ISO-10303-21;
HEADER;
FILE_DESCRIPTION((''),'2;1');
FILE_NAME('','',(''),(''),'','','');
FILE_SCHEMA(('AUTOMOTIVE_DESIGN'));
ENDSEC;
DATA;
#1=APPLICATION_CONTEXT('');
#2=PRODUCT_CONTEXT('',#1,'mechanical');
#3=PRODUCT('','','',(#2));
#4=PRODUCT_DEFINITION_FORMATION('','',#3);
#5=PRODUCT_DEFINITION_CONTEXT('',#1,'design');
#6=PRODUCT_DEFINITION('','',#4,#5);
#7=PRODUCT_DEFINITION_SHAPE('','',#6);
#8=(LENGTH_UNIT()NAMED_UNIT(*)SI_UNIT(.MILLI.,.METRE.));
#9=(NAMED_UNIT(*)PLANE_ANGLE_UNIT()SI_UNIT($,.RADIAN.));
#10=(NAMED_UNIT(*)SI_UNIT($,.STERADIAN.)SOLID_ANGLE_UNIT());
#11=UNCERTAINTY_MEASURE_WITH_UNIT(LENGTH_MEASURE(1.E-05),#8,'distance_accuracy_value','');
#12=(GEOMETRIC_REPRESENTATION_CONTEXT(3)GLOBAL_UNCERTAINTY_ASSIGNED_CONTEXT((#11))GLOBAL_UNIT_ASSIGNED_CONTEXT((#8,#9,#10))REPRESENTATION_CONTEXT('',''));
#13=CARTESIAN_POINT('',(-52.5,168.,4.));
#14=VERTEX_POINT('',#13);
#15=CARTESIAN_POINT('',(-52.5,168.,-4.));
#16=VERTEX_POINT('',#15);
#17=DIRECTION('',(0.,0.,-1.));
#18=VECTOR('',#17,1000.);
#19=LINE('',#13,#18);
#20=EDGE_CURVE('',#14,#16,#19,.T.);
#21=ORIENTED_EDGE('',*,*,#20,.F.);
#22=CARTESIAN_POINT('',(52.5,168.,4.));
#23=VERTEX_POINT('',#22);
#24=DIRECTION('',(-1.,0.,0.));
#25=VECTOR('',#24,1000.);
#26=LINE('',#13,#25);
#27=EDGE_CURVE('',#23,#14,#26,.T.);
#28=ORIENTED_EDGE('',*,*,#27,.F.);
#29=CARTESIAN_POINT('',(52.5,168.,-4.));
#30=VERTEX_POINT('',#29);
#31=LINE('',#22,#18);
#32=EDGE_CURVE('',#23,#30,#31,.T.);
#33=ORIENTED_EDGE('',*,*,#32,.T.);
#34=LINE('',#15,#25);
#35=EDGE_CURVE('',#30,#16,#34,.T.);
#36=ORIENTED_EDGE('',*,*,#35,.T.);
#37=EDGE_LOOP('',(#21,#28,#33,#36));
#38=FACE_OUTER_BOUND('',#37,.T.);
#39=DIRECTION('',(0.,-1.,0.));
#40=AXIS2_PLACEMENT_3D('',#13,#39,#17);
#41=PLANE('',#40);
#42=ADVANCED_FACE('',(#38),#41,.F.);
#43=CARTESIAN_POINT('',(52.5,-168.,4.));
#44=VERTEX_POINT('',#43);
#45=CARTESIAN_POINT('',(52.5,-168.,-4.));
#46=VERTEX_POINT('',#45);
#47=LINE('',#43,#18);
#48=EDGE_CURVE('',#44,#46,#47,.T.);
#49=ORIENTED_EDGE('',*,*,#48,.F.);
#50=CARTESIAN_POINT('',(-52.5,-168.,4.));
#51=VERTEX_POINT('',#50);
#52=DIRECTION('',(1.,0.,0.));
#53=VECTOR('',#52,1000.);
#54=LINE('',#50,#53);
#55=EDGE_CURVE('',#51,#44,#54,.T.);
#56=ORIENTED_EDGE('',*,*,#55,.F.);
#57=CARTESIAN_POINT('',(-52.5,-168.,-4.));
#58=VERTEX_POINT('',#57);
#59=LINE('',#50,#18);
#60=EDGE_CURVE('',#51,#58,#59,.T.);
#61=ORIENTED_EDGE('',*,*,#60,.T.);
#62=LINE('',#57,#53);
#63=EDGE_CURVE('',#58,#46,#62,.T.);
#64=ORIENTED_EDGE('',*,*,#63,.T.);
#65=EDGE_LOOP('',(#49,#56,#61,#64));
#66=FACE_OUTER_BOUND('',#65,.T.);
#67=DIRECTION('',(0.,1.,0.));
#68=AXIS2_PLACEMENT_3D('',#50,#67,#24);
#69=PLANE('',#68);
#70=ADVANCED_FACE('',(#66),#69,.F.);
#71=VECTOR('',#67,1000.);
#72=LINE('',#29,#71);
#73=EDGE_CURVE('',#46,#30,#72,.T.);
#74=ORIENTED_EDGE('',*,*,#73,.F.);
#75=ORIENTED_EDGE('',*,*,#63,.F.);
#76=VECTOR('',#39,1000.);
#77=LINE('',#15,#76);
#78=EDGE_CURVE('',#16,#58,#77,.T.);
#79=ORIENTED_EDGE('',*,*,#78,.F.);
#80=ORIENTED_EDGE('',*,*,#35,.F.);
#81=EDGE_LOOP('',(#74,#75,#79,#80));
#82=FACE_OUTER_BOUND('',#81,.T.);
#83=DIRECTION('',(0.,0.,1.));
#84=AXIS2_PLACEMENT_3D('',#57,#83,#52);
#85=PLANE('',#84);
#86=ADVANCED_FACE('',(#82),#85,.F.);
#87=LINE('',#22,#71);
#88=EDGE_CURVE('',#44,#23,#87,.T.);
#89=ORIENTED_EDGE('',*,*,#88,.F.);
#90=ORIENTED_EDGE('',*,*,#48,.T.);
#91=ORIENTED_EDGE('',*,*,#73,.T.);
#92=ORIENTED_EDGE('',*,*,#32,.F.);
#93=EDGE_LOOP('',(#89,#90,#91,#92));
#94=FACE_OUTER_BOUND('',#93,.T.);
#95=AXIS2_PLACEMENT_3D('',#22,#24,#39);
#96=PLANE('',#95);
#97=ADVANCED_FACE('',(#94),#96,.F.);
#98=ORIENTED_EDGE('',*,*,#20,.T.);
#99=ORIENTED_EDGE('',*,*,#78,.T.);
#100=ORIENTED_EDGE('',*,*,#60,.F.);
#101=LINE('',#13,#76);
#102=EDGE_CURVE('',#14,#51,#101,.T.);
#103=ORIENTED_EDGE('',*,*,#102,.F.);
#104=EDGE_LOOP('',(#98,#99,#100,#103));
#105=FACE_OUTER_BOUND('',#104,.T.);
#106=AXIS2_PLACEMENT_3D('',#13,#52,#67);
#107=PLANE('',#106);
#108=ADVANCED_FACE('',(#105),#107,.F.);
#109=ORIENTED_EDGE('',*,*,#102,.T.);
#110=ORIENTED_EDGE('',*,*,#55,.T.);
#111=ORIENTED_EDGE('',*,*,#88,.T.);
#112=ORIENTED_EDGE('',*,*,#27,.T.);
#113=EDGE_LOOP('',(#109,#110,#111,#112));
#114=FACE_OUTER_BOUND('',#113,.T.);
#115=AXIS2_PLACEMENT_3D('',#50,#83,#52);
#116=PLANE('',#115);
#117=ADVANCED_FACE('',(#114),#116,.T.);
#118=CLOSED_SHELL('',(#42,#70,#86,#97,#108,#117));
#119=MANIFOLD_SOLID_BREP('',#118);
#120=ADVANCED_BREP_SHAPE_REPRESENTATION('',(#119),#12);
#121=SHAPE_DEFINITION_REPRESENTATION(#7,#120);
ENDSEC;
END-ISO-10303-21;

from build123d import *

# Parameters (mm, degrees)
SKETCH1_W           = 105
SKETCH1_H           = 336
BOSS_EXTRUDE1_DEPTH = 4


with BuildPart() as part:
    # Sketch1 → Boss-Extrude1 (new, symmetric)
    with BuildSketch(Plane.XY):
        Rectangle(SKETCH1_W, SKETCH1_H)
    extrude(amount=BOSS_EXTRUDE1_DEPTH, both=True)


solid = part.part
